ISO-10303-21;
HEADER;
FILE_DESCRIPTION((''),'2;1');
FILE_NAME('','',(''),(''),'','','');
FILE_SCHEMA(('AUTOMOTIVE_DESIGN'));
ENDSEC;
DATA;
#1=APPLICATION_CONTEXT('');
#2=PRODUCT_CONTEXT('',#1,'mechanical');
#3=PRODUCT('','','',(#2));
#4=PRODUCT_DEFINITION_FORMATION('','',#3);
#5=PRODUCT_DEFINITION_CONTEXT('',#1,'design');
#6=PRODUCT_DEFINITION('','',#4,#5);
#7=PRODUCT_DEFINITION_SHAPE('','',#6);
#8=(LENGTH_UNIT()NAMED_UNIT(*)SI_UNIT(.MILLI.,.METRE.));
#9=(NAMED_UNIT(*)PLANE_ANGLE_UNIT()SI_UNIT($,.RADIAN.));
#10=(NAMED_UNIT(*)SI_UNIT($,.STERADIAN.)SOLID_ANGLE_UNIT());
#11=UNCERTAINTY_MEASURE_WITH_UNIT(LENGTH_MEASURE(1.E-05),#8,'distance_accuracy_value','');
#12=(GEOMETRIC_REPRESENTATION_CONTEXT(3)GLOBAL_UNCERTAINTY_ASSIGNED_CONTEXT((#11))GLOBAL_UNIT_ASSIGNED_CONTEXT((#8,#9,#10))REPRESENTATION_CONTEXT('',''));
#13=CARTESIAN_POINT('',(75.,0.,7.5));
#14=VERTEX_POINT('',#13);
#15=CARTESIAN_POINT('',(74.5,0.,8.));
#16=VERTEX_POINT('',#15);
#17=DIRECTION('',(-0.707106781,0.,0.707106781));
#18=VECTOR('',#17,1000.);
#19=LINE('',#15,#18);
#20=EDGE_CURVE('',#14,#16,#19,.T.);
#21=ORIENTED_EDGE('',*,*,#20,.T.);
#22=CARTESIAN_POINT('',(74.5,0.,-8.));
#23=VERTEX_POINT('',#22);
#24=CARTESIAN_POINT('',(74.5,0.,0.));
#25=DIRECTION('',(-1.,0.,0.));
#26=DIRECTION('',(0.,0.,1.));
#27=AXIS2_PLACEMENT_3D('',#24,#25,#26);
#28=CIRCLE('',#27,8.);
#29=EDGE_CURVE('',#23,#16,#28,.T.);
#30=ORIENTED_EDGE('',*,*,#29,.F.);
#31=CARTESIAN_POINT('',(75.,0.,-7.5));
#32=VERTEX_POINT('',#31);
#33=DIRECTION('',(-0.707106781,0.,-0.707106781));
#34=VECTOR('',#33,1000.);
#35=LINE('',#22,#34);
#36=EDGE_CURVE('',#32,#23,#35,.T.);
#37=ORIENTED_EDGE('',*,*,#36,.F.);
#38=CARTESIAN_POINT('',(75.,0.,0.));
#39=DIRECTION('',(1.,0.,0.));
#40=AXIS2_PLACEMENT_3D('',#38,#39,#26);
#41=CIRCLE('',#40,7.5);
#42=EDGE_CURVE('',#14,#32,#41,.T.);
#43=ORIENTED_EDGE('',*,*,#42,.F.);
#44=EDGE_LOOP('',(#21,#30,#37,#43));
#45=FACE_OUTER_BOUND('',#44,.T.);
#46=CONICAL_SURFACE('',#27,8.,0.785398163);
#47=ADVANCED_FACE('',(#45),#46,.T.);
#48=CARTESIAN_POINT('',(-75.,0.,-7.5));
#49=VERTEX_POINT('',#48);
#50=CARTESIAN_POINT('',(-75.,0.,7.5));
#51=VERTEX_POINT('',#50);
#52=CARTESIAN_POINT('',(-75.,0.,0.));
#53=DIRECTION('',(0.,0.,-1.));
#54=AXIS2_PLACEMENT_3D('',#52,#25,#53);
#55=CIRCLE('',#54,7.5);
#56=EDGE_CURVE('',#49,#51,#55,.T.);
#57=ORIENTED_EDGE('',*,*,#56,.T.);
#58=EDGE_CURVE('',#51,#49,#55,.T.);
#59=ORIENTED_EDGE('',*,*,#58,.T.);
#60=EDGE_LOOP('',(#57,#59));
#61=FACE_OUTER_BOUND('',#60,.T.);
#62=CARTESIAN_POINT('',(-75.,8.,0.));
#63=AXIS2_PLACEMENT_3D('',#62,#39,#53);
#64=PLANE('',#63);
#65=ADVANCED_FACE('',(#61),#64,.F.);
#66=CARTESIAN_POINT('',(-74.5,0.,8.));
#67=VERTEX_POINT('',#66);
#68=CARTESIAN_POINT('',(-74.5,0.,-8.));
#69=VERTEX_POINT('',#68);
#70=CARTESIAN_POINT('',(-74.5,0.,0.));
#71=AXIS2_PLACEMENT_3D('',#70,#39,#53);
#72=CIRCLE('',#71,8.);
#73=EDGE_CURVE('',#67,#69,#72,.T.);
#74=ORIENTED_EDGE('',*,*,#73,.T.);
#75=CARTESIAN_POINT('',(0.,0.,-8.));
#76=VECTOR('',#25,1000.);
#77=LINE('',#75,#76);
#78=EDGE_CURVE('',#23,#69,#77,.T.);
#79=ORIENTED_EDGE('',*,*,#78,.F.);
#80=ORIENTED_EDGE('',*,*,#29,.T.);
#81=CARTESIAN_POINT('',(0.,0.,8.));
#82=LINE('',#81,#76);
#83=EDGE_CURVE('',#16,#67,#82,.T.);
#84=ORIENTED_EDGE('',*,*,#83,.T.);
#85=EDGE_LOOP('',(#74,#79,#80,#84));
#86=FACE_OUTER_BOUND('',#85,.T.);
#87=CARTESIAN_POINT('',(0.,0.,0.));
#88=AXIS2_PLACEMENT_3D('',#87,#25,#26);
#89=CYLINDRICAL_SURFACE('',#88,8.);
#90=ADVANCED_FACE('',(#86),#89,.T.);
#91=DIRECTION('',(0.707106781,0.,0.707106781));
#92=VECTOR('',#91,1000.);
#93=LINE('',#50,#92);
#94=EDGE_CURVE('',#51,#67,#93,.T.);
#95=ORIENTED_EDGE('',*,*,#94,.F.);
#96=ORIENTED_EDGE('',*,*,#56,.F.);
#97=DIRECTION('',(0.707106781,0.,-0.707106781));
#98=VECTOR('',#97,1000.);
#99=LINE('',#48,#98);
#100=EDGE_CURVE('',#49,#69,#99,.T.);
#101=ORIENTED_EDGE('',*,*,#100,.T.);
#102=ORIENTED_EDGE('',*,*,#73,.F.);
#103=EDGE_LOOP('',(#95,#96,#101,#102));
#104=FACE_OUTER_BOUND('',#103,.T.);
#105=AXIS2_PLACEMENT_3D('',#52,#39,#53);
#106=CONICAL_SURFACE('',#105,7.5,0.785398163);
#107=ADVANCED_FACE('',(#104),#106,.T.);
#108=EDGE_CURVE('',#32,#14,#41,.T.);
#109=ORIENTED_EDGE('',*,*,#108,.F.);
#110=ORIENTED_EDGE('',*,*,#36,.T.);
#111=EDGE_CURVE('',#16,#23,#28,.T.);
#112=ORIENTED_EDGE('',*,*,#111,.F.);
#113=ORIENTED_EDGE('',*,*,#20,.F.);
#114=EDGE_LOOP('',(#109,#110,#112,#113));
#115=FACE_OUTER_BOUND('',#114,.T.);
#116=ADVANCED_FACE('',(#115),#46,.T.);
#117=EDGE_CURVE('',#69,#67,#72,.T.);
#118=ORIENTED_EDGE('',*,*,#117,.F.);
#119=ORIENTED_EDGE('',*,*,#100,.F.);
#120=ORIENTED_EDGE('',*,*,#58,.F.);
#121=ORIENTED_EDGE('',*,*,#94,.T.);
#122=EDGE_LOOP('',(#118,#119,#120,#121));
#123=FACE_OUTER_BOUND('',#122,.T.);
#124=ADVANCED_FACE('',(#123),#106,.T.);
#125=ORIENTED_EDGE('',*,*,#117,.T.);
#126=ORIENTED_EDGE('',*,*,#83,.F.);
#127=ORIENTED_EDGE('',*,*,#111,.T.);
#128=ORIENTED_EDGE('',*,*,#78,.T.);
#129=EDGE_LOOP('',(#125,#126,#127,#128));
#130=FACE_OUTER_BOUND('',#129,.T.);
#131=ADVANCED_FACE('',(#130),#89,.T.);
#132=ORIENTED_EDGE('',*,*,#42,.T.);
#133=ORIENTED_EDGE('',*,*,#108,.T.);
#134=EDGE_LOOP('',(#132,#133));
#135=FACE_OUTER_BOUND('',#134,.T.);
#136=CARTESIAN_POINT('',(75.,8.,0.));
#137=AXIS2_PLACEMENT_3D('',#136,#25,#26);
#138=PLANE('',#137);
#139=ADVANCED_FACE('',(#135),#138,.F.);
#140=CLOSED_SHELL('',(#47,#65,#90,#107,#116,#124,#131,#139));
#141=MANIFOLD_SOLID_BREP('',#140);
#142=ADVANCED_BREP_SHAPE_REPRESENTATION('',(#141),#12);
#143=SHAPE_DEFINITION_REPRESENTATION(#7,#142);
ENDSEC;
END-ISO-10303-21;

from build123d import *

# Parameters (mm, degrees)
SKETCH_1_W     = 150
SKETCH_1_H     = 8
CHAMFER_1_SIZE = 0.5


with BuildPart() as part:
    # 草图1 → 旋转1 (revolve)
    with BuildSketch(Plane.XY, mode=Mode.PRIVATE) as revolve_1_sk:
        with Locations((0, 4)):
            Rectangle(SKETCH_1_W, SKETCH_1_H)
    revolve(revolve_1_sk.sketch.rotate(Axis((0, 0, 0), (1, 0, 0)), 90), axis=Axis((0, 0, 0), (1, 0, 0)))

    # 倒角1
    chamfer_1_edges = [part.edges().sort_by_distance(p)[0] for p in [
        (-75, 0, -8),
        (75, 0, -8),
    ]]
    chamfer(chamfer_1_edges, length=CHAMFER_1_SIZE)


solid = part.part
